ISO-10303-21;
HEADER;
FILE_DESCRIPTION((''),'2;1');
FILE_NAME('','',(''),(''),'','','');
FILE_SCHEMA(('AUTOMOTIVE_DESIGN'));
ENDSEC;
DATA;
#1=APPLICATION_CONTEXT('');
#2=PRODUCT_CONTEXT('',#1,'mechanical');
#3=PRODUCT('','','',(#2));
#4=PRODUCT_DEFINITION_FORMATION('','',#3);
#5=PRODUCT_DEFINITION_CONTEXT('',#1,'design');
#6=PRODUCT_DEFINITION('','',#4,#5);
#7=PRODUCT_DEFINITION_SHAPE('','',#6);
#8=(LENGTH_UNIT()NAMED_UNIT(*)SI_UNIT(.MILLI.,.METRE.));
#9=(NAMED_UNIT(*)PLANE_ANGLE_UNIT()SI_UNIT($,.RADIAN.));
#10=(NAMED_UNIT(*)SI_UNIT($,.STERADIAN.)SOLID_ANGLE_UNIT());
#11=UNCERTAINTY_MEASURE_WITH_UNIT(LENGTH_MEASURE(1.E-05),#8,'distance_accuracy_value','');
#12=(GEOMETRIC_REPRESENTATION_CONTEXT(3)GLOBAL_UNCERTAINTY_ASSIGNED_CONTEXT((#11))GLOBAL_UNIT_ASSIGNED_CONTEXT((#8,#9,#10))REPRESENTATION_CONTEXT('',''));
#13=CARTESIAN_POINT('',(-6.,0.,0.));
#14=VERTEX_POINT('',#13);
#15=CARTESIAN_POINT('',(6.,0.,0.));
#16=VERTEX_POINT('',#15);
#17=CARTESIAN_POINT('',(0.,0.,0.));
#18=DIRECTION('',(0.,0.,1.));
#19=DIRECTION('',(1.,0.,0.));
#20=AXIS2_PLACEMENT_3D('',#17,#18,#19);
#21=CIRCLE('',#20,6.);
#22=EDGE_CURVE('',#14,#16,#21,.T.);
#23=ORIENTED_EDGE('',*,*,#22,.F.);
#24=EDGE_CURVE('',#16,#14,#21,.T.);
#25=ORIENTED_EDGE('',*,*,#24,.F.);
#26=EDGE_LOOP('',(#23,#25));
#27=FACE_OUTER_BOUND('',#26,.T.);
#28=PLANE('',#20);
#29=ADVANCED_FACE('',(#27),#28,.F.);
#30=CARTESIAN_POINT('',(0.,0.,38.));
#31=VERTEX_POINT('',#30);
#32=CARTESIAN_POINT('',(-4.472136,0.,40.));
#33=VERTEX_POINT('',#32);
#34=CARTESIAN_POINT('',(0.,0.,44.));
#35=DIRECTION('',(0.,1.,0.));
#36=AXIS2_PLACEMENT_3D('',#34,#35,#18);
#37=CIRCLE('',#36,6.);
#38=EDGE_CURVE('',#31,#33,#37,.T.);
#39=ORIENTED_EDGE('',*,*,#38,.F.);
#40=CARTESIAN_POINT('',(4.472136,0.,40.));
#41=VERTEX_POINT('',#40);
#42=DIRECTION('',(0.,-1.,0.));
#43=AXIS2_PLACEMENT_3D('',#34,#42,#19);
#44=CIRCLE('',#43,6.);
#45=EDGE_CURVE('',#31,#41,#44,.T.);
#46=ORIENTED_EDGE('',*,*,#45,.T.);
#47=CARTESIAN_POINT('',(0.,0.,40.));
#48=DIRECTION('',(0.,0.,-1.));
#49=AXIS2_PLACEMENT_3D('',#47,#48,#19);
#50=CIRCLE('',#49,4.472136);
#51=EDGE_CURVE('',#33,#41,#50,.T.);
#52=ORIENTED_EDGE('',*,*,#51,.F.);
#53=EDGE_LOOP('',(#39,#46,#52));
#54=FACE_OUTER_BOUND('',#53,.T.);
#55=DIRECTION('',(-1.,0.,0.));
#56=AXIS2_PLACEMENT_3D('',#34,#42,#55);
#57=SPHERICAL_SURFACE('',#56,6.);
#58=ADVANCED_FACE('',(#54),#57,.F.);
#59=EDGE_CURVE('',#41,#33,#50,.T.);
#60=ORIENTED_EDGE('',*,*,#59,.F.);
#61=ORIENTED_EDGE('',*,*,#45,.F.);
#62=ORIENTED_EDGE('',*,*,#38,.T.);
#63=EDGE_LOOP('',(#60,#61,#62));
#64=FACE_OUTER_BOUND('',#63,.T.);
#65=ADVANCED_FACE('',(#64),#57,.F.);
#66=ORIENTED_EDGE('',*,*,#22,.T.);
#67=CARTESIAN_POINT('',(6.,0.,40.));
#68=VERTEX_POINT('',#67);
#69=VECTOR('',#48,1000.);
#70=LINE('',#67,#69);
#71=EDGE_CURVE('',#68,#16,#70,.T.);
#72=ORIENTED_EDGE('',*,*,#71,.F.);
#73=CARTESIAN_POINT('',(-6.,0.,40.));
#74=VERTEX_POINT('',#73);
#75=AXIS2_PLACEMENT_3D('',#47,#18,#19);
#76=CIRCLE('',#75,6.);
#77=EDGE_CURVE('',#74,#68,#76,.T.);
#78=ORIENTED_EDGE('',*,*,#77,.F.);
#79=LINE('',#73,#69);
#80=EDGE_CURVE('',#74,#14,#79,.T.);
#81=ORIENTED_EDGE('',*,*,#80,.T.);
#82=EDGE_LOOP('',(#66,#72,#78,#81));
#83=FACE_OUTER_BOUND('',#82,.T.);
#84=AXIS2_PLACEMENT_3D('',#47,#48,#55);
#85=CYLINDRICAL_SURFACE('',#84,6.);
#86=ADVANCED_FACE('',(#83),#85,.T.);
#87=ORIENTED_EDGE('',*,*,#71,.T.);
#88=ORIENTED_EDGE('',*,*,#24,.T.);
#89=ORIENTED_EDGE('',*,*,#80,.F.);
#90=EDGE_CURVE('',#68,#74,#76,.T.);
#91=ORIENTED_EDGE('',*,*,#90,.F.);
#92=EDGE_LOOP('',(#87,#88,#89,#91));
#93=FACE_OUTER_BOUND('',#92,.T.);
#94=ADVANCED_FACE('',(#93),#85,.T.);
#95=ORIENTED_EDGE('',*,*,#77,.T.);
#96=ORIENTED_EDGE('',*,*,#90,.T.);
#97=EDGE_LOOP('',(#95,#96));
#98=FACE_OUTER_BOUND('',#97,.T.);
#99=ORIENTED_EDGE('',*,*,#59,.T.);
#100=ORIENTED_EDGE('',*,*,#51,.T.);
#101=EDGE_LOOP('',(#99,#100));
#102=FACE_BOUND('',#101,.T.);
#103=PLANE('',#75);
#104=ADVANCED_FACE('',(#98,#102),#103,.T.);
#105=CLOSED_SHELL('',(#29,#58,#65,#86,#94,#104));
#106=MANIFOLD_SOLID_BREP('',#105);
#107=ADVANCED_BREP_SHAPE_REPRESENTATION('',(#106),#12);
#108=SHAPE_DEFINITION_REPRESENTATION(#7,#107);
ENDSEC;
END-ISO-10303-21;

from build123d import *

# Parameters (mm, degrees)
SKETCH_1_R      = 6
EXTRUDE_1_DEPTH = 40


with BuildPart() as part:
    # 草图1 → 凸台-拉伸1 (new body)
    with BuildSketch(Plane.XY):
        Circle(SKETCH_1_R)
    extrude(amount=EXTRUDE_1_DEPTH)

    # 草图2 → 切除-旋转4 (revolve, cut)
    with BuildSketch(Plane(origin=(0, 0, 0), x_dir=(1, 0, 0), z_dir=(0, 1, 0))):
        with BuildLine():
            Line((0, -50), (0, -38))
            ThreePointArc((0, -38), (-6, -44), (0, -50))
        make_face()
    revolve(axis=Axis((0, 0, 50), (0, 0, -1)), mode=Mode.SUBTRACT)


solid = part.part
